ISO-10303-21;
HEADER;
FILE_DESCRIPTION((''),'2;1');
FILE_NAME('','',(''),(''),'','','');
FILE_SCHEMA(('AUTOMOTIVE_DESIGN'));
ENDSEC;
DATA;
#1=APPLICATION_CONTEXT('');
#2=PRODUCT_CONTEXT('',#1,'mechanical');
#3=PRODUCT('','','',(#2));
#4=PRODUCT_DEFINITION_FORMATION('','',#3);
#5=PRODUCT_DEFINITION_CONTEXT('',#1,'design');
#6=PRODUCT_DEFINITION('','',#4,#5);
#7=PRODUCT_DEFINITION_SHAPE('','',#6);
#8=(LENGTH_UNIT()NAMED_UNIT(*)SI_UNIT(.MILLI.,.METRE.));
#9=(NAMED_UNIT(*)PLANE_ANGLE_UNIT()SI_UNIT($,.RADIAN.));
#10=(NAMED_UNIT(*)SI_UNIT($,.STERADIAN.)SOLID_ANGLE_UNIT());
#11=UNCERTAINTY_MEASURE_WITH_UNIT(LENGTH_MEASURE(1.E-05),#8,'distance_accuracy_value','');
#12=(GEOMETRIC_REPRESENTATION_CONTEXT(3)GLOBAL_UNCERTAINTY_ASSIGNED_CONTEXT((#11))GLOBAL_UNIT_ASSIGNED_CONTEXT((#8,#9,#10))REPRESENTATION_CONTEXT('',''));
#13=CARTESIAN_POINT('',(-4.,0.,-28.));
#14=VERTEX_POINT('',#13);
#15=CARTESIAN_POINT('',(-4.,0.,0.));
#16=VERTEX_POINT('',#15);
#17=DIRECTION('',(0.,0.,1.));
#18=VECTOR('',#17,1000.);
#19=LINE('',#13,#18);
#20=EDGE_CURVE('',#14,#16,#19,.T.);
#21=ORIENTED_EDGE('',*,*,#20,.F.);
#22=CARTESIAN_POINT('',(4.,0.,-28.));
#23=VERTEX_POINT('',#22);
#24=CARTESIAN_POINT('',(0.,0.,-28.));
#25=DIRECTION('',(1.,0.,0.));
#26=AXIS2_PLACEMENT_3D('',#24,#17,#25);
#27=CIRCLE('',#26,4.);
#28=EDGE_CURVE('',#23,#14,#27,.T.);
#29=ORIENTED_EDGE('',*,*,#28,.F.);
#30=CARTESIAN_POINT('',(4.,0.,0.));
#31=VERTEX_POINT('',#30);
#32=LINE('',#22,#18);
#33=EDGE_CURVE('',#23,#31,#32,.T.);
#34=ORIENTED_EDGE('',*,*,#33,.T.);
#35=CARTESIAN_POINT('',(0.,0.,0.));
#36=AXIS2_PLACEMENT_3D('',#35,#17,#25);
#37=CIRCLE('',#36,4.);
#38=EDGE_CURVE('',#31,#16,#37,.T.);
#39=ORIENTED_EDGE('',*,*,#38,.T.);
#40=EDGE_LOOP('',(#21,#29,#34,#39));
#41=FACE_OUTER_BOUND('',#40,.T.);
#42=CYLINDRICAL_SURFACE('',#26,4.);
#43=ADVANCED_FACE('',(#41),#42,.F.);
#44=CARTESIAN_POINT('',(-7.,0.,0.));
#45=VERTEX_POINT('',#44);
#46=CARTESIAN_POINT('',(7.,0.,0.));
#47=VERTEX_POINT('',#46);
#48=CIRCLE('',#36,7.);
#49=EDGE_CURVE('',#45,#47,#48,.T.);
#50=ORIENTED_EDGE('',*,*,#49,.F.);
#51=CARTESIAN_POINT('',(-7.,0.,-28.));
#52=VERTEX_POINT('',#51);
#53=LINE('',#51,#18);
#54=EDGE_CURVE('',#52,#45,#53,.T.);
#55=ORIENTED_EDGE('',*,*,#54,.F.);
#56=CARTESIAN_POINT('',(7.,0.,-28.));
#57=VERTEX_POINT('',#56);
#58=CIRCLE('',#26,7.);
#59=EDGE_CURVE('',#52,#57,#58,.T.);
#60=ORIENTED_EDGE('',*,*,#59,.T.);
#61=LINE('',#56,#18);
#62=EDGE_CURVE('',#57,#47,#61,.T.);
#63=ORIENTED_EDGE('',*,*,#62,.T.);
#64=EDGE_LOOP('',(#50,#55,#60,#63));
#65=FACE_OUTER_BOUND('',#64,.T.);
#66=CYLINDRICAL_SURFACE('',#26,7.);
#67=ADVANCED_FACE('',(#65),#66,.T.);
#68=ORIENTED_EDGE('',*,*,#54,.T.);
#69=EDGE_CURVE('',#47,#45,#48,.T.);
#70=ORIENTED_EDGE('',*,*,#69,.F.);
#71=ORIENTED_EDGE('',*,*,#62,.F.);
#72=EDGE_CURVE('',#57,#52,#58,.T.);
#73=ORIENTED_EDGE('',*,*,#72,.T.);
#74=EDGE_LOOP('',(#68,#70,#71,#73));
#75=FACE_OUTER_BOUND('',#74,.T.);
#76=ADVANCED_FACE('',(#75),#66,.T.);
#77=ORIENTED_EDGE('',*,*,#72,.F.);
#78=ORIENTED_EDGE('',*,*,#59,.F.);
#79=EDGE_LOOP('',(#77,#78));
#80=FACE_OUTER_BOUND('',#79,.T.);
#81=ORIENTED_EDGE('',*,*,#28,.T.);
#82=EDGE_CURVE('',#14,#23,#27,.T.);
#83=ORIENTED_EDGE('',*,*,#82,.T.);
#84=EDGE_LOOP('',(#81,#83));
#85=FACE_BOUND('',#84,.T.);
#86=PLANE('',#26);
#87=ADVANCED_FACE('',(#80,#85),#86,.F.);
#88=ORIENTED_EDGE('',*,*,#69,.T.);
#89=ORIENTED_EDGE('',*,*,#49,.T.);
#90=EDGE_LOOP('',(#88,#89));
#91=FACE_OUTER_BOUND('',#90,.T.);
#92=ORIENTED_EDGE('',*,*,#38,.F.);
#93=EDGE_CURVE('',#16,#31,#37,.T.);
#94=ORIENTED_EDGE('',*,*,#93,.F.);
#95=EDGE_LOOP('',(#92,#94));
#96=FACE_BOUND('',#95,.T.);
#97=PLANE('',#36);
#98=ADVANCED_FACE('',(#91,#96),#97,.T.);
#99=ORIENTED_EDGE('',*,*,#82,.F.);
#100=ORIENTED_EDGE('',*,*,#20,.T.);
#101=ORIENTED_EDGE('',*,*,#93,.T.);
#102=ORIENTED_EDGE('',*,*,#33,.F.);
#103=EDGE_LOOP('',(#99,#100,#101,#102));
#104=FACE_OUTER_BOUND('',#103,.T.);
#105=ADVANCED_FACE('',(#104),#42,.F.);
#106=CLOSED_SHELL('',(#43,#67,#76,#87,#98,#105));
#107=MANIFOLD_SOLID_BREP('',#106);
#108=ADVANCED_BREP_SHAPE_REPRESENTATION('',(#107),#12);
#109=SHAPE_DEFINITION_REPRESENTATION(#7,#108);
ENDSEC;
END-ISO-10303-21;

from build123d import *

# Parameters (mm, degrees)
SKETCH1_R           = 7
SKETCH1_R_2         = 4
BOSS_EXTRUDE1_DEPTH = 28


with BuildPart() as part:
    # Sketch1 → Boss-Extrude1 (new body)
    with BuildSketch(Plane.XY):
        Circle(SKETCH1_R)
        Circle(SKETCH1_R_2, mode=Mode.SUBTRACT)
    extrude(amount=-BOSS_EXTRUDE1_DEPTH)


solid = part.part
